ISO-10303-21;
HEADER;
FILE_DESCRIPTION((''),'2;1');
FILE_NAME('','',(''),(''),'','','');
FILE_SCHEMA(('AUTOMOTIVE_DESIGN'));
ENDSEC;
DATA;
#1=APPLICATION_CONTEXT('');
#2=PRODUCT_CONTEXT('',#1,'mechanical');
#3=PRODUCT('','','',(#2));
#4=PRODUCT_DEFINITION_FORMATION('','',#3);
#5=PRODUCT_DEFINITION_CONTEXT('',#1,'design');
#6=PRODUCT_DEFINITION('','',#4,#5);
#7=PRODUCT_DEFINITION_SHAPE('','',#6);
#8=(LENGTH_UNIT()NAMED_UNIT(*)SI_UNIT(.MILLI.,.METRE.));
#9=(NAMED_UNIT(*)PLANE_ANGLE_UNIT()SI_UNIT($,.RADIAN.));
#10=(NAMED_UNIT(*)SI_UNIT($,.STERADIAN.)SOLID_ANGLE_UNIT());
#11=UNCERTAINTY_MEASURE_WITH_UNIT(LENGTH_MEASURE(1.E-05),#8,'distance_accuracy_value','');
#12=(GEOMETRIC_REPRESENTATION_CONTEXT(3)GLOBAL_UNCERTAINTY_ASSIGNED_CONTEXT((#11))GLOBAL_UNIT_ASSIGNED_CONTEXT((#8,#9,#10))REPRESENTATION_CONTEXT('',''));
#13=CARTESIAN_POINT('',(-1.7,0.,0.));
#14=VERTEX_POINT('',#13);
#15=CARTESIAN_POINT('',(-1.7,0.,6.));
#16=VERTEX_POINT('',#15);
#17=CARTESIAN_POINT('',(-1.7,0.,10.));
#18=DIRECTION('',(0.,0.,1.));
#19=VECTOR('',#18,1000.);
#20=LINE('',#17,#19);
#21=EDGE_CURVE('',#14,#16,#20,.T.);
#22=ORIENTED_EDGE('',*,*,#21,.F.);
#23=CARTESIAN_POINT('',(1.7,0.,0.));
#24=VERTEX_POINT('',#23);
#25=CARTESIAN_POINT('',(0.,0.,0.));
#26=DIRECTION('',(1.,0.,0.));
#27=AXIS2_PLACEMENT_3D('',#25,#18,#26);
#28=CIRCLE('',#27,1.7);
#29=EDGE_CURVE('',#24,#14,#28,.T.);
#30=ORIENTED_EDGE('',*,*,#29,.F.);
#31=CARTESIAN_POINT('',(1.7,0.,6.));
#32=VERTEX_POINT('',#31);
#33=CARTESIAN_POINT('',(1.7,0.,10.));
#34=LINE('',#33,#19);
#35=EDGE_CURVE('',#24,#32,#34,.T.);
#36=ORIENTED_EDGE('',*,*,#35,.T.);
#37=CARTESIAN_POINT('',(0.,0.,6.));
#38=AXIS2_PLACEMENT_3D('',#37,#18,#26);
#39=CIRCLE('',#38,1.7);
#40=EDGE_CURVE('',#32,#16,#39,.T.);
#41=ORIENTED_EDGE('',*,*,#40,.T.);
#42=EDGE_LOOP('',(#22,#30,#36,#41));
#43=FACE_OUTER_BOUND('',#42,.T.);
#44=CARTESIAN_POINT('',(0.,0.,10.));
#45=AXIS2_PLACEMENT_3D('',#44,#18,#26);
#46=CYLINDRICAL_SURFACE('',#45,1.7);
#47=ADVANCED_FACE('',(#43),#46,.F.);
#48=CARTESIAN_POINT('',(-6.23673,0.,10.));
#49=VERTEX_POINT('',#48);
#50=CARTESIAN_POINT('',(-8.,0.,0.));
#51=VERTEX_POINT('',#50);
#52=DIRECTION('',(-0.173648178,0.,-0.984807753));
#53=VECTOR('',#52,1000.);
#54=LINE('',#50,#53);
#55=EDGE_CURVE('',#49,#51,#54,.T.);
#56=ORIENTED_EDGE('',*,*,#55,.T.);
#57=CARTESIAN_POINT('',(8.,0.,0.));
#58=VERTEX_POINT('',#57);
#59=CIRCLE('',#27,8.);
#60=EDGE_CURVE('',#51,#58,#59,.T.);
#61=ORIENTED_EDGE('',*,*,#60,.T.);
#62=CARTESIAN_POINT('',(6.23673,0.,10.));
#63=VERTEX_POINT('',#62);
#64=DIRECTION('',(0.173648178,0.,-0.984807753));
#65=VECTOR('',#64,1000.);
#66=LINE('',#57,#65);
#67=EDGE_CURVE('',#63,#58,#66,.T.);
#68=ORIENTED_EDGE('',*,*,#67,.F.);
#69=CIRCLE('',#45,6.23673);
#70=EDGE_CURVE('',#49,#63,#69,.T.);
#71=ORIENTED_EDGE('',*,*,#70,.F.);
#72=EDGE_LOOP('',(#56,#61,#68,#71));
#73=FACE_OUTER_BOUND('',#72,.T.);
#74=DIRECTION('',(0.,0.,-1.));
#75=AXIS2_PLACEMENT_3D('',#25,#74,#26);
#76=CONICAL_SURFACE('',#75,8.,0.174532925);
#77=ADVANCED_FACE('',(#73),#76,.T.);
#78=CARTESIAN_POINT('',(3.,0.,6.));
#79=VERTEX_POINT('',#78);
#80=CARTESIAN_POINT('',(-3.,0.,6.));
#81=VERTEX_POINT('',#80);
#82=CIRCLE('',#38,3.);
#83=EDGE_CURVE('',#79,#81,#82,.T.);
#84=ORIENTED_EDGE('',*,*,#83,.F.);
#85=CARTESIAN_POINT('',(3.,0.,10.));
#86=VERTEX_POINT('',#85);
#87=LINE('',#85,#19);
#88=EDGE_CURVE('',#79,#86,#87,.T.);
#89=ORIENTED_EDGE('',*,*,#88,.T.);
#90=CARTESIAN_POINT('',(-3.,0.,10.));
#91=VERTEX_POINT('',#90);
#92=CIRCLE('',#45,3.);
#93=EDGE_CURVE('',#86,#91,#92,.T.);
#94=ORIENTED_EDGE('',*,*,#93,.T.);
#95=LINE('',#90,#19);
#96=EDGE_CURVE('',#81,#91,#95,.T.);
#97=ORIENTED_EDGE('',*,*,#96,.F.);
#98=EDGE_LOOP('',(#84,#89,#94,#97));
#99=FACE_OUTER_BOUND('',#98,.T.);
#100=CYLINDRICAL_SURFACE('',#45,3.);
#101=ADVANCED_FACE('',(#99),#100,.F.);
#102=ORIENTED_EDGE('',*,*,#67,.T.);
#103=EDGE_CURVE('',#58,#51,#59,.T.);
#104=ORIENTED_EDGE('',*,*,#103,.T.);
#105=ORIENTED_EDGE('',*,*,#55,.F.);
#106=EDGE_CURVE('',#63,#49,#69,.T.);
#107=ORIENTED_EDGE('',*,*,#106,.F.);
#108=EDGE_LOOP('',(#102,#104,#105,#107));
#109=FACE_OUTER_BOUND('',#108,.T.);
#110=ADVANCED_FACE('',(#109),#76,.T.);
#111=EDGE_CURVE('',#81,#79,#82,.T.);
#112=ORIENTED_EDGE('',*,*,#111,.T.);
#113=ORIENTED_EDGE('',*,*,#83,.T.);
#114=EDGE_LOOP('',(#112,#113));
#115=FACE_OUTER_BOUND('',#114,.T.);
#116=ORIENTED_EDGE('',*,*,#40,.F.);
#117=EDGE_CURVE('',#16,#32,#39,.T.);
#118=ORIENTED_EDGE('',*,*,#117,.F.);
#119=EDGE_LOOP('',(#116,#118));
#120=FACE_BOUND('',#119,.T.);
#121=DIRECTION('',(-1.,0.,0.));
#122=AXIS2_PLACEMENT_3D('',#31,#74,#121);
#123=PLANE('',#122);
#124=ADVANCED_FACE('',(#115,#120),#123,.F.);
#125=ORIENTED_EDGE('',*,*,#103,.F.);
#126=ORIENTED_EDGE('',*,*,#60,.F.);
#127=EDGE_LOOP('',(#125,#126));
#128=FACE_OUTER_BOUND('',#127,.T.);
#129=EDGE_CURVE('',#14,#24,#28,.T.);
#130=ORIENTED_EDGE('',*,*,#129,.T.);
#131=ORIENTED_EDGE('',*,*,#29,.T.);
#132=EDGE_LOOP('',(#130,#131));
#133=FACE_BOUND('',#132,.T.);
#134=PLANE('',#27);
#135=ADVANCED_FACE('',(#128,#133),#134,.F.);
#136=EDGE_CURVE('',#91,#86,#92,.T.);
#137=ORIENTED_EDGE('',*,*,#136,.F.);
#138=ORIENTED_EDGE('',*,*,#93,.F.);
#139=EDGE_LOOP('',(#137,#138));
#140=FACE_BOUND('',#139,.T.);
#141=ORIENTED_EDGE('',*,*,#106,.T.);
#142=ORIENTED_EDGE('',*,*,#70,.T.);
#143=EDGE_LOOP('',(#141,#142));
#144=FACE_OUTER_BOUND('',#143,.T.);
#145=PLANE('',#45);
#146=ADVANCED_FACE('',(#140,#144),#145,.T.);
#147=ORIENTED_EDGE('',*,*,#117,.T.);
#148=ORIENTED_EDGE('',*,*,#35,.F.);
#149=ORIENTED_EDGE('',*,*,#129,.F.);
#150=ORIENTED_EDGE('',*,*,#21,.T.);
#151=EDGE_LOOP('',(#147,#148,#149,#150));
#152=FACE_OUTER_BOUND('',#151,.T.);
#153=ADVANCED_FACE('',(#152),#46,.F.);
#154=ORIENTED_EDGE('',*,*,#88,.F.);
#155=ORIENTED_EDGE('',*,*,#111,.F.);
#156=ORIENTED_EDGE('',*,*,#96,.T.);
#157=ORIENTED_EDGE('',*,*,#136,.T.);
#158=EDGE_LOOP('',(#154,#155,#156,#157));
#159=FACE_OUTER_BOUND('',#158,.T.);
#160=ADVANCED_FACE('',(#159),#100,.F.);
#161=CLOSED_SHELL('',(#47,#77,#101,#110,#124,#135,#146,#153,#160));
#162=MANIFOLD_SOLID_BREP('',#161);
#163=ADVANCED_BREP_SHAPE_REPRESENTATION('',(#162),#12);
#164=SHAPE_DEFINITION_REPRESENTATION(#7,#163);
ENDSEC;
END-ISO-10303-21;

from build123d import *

# Parameters (mm, degrees)
SKETCH_1_R                = 8
EXTRUDE_1_DEPTH           = 10
EXTRUDE_1_TAPER           = 10
HOLE_WIZARD_1_D           = 3.4
HOLE_WIZARD_1_CBORE_D     = 6
HOLE_WIZARD_1_CBORE_DEPTH = 4


with BuildPart() as part:
    # 草图1 → 凸台-拉伸1 (new body)
    with BuildSketch(Plane.XY):
        Circle(SKETCH_1_R)
    extrude(amount=EXTRUDE_1_DEPTH, taper=EXTRUDE_1_TAPER)

    # 打孔尺寸(%根据)内六角圆柱头螺钉的类型1 (through all)
    with Locations(Plane.XY.offset(10)):
        with Locations((0, 0)):
            CounterBoreHole(HOLE_WIZARD_1_D / 2, HOLE_WIZARD_1_CBORE_D / 2, HOLE_WIZARD_1_CBORE_DEPTH)


solid = part.part
